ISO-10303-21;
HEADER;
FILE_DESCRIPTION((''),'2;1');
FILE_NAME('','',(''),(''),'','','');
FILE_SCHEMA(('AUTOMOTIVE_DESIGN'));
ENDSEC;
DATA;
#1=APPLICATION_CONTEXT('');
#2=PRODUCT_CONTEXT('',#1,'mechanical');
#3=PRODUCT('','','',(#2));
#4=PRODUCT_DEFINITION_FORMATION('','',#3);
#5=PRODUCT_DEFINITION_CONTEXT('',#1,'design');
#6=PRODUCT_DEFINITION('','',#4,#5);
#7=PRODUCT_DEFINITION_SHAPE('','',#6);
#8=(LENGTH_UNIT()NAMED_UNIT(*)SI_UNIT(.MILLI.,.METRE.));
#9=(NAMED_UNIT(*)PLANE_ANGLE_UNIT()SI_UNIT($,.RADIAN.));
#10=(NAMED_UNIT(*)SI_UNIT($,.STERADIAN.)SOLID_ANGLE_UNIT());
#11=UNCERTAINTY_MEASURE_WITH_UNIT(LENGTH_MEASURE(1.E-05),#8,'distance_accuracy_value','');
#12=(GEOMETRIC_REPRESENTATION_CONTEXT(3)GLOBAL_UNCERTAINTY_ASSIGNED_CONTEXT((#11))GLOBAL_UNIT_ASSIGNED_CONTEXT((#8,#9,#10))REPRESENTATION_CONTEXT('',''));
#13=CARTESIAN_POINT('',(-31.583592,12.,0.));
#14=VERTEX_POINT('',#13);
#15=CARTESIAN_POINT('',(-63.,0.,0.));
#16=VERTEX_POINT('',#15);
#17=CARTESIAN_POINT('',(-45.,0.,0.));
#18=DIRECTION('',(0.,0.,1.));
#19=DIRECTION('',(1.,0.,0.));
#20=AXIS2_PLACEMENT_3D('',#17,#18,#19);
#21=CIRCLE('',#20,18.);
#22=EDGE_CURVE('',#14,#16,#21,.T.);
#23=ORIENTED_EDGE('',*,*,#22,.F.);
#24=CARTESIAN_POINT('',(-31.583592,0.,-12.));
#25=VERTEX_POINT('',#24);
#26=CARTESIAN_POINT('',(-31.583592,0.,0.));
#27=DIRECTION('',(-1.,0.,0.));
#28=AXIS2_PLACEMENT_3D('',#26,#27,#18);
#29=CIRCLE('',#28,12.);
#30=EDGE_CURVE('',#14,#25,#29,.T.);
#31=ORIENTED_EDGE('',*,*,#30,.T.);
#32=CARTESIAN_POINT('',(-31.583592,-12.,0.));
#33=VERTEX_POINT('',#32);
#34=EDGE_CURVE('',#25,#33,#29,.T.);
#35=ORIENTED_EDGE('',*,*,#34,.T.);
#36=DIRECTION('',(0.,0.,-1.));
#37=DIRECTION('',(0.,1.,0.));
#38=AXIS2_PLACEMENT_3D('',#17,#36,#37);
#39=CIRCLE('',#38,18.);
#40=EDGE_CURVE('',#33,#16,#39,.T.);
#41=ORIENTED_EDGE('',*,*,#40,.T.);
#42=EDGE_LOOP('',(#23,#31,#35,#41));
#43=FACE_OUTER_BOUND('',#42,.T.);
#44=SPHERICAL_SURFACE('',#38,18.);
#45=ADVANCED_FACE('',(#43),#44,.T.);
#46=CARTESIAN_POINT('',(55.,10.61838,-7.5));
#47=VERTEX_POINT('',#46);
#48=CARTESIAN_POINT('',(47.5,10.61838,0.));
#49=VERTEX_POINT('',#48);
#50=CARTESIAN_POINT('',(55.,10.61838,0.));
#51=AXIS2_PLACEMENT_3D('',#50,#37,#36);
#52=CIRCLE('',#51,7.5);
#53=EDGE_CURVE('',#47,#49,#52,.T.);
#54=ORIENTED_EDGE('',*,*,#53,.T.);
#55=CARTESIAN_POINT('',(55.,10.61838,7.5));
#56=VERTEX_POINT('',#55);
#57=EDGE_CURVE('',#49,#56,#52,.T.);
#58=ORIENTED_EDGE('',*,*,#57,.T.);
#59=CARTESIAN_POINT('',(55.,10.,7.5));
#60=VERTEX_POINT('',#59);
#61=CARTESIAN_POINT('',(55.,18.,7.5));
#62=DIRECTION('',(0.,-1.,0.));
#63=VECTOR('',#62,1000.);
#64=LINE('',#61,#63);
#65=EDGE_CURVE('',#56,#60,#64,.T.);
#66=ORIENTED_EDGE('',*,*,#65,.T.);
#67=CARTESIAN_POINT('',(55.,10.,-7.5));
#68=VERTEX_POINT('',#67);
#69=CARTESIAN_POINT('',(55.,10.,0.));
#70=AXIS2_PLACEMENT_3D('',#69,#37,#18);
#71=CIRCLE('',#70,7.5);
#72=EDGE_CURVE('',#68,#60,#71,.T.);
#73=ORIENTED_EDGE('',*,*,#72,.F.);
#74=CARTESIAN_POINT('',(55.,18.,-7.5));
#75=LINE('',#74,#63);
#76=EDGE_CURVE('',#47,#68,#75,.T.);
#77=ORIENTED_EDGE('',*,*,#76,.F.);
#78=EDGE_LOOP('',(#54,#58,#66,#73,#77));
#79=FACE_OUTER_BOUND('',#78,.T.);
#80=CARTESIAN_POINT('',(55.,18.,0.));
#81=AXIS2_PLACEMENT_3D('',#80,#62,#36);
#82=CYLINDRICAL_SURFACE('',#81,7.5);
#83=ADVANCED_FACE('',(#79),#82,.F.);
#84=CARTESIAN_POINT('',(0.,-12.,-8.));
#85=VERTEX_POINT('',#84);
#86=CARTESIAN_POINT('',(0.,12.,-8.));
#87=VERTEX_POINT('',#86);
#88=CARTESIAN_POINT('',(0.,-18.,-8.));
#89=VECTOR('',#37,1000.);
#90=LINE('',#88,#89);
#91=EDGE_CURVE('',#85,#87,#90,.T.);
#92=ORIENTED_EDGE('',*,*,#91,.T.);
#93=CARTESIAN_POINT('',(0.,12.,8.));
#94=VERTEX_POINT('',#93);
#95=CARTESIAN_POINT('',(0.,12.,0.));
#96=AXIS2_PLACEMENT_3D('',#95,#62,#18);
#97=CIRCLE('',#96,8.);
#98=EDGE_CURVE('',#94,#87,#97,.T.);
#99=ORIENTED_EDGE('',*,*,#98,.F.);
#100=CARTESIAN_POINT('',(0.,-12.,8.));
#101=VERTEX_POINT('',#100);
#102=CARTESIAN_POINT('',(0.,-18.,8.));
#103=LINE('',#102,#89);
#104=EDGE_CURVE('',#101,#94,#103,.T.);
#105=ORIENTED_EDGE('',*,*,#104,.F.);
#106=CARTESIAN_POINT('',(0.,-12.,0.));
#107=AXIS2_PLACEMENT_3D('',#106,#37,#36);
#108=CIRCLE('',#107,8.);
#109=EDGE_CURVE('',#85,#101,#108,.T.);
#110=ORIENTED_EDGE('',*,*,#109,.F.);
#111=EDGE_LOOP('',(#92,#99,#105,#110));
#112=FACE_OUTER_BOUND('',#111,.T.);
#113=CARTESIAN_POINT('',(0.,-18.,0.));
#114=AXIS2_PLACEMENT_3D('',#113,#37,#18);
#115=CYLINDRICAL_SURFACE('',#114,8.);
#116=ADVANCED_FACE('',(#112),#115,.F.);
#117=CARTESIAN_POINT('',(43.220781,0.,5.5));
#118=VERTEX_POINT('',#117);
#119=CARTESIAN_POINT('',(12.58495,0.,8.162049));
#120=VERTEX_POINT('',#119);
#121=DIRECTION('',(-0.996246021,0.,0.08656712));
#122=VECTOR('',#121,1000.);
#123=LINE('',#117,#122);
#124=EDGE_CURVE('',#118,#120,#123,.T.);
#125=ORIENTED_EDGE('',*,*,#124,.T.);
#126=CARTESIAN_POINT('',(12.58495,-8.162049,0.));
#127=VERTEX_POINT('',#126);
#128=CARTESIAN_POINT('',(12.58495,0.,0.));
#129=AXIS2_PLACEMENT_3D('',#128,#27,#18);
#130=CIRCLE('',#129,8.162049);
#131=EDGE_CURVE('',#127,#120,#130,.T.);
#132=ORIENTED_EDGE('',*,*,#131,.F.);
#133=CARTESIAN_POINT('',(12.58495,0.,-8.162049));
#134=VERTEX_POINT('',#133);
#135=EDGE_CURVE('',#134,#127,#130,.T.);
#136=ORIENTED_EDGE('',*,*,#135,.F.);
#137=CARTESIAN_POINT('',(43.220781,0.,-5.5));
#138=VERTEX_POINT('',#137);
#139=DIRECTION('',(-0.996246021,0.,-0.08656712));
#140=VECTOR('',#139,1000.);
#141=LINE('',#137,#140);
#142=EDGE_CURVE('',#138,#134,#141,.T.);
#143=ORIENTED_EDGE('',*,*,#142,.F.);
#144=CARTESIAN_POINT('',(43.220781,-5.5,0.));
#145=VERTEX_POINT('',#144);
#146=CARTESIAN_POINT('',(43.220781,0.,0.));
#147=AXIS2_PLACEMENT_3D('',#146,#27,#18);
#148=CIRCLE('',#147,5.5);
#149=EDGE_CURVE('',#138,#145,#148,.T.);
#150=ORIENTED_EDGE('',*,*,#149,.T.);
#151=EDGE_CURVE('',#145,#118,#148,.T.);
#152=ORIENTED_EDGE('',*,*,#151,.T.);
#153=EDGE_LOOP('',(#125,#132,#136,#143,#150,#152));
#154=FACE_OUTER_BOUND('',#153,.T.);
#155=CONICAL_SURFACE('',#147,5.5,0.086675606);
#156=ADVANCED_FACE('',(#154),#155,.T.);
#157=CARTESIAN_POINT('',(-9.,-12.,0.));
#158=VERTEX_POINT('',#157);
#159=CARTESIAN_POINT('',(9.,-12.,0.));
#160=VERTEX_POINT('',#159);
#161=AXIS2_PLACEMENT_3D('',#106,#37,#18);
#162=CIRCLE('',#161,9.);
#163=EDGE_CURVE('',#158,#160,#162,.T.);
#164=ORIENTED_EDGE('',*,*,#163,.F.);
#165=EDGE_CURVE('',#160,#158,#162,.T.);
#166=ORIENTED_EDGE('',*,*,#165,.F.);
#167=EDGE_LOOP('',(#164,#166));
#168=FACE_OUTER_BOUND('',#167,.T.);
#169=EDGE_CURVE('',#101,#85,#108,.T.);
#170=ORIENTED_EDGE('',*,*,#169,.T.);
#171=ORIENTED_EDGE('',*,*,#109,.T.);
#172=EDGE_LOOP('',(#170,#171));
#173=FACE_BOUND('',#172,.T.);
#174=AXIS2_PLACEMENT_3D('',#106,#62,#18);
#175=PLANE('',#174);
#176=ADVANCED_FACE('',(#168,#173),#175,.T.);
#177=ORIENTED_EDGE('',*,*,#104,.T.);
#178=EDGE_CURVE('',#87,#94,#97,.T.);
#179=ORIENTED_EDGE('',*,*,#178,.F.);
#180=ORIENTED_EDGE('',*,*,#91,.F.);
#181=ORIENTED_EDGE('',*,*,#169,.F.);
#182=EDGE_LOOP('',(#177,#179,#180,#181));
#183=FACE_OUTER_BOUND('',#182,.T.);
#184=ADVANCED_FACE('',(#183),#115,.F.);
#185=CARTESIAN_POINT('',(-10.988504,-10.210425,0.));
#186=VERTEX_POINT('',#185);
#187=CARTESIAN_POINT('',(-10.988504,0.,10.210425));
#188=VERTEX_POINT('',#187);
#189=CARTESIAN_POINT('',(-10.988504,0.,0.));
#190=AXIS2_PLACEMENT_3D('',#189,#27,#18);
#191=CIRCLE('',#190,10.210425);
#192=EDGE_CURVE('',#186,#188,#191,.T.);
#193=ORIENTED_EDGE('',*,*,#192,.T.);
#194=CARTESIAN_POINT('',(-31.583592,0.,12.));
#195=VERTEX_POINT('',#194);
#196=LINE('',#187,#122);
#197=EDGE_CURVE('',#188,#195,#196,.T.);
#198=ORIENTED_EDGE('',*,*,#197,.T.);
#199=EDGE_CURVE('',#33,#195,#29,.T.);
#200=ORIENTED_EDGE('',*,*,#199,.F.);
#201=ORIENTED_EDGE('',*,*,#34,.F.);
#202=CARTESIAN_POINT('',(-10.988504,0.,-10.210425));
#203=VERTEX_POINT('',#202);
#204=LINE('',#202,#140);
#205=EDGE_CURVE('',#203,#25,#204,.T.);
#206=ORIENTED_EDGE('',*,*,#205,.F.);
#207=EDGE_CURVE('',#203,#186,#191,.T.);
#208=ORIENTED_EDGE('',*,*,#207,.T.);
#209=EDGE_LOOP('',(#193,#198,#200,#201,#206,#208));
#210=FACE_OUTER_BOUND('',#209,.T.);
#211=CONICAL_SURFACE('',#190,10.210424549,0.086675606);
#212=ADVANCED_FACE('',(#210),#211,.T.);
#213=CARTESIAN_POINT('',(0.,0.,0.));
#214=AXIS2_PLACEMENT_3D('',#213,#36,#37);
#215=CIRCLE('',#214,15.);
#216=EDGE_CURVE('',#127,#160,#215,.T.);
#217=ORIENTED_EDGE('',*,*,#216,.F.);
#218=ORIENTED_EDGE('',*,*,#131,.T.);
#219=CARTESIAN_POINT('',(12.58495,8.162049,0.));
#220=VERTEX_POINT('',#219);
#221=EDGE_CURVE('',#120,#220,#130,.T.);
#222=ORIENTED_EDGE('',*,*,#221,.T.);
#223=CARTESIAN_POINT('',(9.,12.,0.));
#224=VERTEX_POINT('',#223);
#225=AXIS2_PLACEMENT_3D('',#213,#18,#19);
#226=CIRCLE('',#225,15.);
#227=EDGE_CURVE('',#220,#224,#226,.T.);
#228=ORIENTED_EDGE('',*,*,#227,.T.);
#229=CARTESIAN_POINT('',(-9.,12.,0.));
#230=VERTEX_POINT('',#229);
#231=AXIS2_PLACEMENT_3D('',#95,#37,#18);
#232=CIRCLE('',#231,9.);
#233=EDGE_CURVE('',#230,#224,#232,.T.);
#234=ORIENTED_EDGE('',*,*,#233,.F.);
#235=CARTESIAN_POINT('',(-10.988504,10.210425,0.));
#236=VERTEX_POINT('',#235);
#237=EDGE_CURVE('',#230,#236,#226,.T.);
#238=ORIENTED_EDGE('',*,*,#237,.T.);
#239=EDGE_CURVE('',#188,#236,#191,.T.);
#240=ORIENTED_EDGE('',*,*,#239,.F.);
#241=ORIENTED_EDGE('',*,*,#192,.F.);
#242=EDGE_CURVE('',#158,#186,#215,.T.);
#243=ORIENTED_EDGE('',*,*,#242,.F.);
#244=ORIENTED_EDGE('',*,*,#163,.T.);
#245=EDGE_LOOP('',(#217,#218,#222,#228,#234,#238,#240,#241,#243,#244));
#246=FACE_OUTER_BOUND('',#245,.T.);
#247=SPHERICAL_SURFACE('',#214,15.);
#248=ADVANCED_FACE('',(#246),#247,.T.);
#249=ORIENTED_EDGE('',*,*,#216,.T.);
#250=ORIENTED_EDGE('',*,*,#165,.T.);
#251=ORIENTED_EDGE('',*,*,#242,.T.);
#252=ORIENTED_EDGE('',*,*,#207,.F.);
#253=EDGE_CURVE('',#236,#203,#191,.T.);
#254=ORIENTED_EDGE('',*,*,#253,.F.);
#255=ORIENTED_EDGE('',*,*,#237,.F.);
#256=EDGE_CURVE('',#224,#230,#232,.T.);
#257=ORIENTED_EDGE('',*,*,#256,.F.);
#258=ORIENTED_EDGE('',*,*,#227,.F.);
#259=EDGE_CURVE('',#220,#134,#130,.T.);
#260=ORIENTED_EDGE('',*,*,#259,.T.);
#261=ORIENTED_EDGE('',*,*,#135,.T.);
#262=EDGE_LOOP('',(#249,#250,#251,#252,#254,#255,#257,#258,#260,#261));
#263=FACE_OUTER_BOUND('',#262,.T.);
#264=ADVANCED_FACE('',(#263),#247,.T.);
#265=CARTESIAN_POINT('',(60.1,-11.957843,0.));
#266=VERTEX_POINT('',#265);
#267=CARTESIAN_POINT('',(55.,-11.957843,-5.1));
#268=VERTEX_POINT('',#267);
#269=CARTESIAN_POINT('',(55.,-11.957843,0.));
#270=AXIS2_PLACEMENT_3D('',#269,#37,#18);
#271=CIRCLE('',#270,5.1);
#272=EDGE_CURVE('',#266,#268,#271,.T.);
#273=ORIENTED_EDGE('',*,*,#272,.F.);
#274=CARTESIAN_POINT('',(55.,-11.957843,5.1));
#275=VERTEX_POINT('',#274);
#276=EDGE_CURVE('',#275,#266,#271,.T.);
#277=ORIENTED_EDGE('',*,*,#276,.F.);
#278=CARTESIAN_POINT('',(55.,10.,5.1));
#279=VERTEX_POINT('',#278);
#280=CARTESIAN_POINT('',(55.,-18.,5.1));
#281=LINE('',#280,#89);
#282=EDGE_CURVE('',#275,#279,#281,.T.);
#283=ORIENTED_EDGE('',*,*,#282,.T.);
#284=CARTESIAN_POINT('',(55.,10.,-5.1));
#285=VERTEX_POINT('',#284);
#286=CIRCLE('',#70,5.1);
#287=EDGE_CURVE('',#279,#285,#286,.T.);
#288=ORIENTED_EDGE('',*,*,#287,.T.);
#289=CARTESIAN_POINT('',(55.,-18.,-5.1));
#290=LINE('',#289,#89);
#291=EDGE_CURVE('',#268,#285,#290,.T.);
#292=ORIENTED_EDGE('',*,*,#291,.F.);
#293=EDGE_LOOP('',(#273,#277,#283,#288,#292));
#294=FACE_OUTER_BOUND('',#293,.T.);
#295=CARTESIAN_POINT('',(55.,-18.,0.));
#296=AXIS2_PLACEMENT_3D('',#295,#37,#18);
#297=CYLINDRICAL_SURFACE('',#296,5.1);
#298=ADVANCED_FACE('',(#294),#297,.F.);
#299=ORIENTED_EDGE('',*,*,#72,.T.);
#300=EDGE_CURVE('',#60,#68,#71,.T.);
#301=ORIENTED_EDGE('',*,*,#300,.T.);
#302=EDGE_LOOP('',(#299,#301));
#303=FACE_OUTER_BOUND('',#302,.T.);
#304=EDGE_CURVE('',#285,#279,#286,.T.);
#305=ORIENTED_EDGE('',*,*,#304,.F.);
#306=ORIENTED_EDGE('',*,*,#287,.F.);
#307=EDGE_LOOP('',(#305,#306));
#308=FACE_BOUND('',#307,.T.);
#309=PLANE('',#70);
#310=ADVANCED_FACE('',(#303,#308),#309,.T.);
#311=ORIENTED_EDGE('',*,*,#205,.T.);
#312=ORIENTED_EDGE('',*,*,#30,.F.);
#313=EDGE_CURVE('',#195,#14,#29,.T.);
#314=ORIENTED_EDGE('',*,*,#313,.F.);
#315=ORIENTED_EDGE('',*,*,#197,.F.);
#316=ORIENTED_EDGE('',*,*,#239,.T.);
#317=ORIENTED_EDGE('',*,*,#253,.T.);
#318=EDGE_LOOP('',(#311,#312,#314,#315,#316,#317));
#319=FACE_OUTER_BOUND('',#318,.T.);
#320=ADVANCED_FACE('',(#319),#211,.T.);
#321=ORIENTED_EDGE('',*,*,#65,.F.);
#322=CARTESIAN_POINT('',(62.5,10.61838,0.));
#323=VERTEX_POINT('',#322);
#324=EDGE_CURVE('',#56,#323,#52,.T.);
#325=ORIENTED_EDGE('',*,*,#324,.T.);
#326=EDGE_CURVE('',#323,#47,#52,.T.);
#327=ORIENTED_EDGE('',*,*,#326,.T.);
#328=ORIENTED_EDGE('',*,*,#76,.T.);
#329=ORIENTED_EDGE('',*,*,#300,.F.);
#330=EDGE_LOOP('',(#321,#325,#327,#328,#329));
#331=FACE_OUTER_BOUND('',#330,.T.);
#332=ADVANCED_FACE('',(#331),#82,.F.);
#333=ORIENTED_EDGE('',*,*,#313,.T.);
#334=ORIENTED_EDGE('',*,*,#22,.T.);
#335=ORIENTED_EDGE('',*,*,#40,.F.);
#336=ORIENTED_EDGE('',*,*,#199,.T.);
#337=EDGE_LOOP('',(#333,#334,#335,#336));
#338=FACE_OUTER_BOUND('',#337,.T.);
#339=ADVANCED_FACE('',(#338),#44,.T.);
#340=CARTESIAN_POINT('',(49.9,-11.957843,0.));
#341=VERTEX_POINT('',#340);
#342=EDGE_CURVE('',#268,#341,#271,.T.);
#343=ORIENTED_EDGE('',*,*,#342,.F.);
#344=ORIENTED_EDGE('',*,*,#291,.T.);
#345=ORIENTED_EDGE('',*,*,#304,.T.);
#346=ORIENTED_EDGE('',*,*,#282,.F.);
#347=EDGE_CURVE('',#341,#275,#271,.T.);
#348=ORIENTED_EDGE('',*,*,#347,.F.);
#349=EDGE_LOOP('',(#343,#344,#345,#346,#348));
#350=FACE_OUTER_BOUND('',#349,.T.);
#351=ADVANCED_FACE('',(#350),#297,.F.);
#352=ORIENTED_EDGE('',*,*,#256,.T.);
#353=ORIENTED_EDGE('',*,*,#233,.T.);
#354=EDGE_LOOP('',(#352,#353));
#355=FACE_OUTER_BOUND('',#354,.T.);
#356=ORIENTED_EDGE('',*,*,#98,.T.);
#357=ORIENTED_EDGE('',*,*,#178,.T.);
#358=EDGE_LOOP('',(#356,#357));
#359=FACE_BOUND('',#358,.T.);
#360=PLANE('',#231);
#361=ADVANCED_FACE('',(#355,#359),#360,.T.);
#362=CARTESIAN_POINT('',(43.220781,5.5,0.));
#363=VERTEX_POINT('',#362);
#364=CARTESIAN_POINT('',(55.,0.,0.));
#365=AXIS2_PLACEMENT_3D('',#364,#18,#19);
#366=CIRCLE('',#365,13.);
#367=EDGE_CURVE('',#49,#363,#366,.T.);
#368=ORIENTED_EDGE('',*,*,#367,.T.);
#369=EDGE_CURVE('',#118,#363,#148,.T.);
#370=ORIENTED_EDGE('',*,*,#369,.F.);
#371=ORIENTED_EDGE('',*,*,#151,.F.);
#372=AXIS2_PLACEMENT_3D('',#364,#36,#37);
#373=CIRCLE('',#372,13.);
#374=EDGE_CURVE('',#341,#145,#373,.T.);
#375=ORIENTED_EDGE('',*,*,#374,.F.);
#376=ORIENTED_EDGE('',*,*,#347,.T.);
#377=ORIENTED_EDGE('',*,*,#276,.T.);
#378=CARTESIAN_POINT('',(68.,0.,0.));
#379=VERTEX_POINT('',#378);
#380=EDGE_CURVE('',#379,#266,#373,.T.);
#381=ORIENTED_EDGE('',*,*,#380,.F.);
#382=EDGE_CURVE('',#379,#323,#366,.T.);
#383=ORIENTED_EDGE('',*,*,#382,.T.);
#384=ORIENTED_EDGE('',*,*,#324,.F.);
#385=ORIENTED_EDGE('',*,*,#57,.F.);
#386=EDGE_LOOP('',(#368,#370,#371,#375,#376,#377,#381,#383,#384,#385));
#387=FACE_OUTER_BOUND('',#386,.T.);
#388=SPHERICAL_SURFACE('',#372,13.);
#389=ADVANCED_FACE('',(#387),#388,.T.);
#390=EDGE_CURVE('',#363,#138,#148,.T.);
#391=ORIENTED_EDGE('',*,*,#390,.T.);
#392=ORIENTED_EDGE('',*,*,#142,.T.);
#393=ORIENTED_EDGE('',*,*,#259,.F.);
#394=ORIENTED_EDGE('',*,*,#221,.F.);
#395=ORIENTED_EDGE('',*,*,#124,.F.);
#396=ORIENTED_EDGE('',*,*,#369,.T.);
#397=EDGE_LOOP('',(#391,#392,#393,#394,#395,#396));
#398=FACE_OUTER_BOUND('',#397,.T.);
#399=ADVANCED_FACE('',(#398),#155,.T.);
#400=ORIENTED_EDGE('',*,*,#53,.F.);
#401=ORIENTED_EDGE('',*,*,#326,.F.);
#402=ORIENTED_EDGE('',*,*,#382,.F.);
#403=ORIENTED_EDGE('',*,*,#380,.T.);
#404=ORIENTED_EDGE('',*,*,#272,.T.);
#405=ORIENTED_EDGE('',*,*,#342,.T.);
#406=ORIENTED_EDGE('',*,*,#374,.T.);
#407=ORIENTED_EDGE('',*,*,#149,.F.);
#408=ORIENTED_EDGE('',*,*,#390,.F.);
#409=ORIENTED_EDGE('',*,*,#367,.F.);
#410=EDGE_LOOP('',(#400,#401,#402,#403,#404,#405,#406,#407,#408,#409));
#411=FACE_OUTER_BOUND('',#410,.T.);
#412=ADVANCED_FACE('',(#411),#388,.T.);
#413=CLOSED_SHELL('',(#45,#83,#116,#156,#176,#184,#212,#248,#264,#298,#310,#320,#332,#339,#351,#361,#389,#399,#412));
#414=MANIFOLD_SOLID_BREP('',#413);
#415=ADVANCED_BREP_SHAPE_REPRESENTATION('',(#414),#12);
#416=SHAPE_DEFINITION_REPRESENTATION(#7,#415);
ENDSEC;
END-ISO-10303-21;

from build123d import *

# Parameters (mm, degrees)
BORE_13_DEPTH                     = 73.608539443
BORE_13_DEPTH_BACK                = 73.608539443
BORE_13_SKETCH_R                  = 8
RECESS_START                      = 10
RECESS_15_SKETCH_R                = 7.5
RECESS_15X10_DEPTH                = 63.608539443
COUNTERBORE_START                 = 12
COUNTERBORE_18_SKETCH_R           = 9
COUNTERBORE_18X12_DEPTH           = 61.608539443
HANDLE_SHANK_BORE_10_2_DEPTH      = 73.608539443
HANDLE_SHANK_BORE_10_2_DEPTH_BACK = 73.608539443
SKETCH6_R                         = 5.1


with BuildPart() as part:
    # Handle Profile Sketch → Handle Body Revolve (revolve)
    with BuildSketch(Plane.XY):
        with BuildLine():
            Line((-31.583592135, 12), (-10.988504472, 10.210424549))
            ThreePointArc((-10.988504472, 10.210424549), (1.298506798, 14.943690311), (12.58494961, 8.162048965))
            Line((12.58494961, 8.162048965), (43.220781011, 5.5))
            ThreePointArc((43.220781011, 5.5), (57.816926795, 12.691135624), (68, 0))
            Line((68, 0), (-63, 0))
            ThreePointArc((-63, 0), (-51.422797616, 16.815102461), (-31.583592135, 12))
        make_face()
    revolve(axis=Axis((-65.491317505, 0, 0), (1, 0, 0)))

    # Bore Ø13 Sketch → Bore Ø13 (cut, two sides: drawn at the far end of the back side and taken through both)
    with BuildSketch(Plane(origin=(0, 0, 0), x_dir=(1, 0, 0), z_dir=(0, 1, 0)).offset(-BORE_13_DEPTH_BACK)):
        with Locations(Location((0, 0, 0), (0, 0, 270))):
            Circle(BORE_13_SKETCH_R)
    extrude(amount=BORE_13_DEPTH + BORE_13_DEPTH_BACK, mode=Mode.SUBTRACT)

    # Recess Ø15 Sketch → Recess Ø15x10 (cut, through all)
    with BuildSketch(Plane(origin=(0, 0, 0), x_dir=(1, 0, 0), z_dir=(0, 1, 0)).offset(RECESS_START)):
        with Locations(Location((55, 0, 0), (0, 0, 90))):
            Circle(RECESS_15_SKETCH_R)
    extrude(amount=RECESS_15X10_DEPTH, mode=Mode.SUBTRACT)

    # Counterbore Ø18 Sketch → Counterbore Ø18x12 (cut, through all)
    with BuildSketch(Plane(origin=(0, 0, 0), x_dir=(1, 0, 0), z_dir=(0, 1, 0)).offset(COUNTERBORE_START)):
        Circle(COUNTERBORE_18_SKETCH_R)
    counterbore_18x12 = extrude(amount=COUNTERBORE_18X12_DEPTH, mode=Mode.SUBTRACT)

    # Counterbore Mirror: Counterbore Ø18x12 across plane
    add(counterbore_18x12.mirror(Plane.ZX), mode=Mode.SUBTRACT)

    # Sketch6 → Handle Shank Bore Ø10.2 (cut, two sides: drawn at the far end of the back side and taken through both)
    with BuildSketch(Plane(origin=(0, 0, 0), x_dir=(1, 0, 0), z_dir=(0, 1, 0)).offset(-HANDLE_SHANK_BORE_10_2_DEPTH_BACK)):
        with Locations(Location((55, 0, 0), (0, 0, 270))):
            Circle(SKETCH6_R)
    extrude(amount=HANDLE_SHANK_BORE_10_2_DEPTH + HANDLE_SHANK_BORE_10_2_DEPTH_BACK, mode=Mode.SUBTRACT)


solid = part.part
